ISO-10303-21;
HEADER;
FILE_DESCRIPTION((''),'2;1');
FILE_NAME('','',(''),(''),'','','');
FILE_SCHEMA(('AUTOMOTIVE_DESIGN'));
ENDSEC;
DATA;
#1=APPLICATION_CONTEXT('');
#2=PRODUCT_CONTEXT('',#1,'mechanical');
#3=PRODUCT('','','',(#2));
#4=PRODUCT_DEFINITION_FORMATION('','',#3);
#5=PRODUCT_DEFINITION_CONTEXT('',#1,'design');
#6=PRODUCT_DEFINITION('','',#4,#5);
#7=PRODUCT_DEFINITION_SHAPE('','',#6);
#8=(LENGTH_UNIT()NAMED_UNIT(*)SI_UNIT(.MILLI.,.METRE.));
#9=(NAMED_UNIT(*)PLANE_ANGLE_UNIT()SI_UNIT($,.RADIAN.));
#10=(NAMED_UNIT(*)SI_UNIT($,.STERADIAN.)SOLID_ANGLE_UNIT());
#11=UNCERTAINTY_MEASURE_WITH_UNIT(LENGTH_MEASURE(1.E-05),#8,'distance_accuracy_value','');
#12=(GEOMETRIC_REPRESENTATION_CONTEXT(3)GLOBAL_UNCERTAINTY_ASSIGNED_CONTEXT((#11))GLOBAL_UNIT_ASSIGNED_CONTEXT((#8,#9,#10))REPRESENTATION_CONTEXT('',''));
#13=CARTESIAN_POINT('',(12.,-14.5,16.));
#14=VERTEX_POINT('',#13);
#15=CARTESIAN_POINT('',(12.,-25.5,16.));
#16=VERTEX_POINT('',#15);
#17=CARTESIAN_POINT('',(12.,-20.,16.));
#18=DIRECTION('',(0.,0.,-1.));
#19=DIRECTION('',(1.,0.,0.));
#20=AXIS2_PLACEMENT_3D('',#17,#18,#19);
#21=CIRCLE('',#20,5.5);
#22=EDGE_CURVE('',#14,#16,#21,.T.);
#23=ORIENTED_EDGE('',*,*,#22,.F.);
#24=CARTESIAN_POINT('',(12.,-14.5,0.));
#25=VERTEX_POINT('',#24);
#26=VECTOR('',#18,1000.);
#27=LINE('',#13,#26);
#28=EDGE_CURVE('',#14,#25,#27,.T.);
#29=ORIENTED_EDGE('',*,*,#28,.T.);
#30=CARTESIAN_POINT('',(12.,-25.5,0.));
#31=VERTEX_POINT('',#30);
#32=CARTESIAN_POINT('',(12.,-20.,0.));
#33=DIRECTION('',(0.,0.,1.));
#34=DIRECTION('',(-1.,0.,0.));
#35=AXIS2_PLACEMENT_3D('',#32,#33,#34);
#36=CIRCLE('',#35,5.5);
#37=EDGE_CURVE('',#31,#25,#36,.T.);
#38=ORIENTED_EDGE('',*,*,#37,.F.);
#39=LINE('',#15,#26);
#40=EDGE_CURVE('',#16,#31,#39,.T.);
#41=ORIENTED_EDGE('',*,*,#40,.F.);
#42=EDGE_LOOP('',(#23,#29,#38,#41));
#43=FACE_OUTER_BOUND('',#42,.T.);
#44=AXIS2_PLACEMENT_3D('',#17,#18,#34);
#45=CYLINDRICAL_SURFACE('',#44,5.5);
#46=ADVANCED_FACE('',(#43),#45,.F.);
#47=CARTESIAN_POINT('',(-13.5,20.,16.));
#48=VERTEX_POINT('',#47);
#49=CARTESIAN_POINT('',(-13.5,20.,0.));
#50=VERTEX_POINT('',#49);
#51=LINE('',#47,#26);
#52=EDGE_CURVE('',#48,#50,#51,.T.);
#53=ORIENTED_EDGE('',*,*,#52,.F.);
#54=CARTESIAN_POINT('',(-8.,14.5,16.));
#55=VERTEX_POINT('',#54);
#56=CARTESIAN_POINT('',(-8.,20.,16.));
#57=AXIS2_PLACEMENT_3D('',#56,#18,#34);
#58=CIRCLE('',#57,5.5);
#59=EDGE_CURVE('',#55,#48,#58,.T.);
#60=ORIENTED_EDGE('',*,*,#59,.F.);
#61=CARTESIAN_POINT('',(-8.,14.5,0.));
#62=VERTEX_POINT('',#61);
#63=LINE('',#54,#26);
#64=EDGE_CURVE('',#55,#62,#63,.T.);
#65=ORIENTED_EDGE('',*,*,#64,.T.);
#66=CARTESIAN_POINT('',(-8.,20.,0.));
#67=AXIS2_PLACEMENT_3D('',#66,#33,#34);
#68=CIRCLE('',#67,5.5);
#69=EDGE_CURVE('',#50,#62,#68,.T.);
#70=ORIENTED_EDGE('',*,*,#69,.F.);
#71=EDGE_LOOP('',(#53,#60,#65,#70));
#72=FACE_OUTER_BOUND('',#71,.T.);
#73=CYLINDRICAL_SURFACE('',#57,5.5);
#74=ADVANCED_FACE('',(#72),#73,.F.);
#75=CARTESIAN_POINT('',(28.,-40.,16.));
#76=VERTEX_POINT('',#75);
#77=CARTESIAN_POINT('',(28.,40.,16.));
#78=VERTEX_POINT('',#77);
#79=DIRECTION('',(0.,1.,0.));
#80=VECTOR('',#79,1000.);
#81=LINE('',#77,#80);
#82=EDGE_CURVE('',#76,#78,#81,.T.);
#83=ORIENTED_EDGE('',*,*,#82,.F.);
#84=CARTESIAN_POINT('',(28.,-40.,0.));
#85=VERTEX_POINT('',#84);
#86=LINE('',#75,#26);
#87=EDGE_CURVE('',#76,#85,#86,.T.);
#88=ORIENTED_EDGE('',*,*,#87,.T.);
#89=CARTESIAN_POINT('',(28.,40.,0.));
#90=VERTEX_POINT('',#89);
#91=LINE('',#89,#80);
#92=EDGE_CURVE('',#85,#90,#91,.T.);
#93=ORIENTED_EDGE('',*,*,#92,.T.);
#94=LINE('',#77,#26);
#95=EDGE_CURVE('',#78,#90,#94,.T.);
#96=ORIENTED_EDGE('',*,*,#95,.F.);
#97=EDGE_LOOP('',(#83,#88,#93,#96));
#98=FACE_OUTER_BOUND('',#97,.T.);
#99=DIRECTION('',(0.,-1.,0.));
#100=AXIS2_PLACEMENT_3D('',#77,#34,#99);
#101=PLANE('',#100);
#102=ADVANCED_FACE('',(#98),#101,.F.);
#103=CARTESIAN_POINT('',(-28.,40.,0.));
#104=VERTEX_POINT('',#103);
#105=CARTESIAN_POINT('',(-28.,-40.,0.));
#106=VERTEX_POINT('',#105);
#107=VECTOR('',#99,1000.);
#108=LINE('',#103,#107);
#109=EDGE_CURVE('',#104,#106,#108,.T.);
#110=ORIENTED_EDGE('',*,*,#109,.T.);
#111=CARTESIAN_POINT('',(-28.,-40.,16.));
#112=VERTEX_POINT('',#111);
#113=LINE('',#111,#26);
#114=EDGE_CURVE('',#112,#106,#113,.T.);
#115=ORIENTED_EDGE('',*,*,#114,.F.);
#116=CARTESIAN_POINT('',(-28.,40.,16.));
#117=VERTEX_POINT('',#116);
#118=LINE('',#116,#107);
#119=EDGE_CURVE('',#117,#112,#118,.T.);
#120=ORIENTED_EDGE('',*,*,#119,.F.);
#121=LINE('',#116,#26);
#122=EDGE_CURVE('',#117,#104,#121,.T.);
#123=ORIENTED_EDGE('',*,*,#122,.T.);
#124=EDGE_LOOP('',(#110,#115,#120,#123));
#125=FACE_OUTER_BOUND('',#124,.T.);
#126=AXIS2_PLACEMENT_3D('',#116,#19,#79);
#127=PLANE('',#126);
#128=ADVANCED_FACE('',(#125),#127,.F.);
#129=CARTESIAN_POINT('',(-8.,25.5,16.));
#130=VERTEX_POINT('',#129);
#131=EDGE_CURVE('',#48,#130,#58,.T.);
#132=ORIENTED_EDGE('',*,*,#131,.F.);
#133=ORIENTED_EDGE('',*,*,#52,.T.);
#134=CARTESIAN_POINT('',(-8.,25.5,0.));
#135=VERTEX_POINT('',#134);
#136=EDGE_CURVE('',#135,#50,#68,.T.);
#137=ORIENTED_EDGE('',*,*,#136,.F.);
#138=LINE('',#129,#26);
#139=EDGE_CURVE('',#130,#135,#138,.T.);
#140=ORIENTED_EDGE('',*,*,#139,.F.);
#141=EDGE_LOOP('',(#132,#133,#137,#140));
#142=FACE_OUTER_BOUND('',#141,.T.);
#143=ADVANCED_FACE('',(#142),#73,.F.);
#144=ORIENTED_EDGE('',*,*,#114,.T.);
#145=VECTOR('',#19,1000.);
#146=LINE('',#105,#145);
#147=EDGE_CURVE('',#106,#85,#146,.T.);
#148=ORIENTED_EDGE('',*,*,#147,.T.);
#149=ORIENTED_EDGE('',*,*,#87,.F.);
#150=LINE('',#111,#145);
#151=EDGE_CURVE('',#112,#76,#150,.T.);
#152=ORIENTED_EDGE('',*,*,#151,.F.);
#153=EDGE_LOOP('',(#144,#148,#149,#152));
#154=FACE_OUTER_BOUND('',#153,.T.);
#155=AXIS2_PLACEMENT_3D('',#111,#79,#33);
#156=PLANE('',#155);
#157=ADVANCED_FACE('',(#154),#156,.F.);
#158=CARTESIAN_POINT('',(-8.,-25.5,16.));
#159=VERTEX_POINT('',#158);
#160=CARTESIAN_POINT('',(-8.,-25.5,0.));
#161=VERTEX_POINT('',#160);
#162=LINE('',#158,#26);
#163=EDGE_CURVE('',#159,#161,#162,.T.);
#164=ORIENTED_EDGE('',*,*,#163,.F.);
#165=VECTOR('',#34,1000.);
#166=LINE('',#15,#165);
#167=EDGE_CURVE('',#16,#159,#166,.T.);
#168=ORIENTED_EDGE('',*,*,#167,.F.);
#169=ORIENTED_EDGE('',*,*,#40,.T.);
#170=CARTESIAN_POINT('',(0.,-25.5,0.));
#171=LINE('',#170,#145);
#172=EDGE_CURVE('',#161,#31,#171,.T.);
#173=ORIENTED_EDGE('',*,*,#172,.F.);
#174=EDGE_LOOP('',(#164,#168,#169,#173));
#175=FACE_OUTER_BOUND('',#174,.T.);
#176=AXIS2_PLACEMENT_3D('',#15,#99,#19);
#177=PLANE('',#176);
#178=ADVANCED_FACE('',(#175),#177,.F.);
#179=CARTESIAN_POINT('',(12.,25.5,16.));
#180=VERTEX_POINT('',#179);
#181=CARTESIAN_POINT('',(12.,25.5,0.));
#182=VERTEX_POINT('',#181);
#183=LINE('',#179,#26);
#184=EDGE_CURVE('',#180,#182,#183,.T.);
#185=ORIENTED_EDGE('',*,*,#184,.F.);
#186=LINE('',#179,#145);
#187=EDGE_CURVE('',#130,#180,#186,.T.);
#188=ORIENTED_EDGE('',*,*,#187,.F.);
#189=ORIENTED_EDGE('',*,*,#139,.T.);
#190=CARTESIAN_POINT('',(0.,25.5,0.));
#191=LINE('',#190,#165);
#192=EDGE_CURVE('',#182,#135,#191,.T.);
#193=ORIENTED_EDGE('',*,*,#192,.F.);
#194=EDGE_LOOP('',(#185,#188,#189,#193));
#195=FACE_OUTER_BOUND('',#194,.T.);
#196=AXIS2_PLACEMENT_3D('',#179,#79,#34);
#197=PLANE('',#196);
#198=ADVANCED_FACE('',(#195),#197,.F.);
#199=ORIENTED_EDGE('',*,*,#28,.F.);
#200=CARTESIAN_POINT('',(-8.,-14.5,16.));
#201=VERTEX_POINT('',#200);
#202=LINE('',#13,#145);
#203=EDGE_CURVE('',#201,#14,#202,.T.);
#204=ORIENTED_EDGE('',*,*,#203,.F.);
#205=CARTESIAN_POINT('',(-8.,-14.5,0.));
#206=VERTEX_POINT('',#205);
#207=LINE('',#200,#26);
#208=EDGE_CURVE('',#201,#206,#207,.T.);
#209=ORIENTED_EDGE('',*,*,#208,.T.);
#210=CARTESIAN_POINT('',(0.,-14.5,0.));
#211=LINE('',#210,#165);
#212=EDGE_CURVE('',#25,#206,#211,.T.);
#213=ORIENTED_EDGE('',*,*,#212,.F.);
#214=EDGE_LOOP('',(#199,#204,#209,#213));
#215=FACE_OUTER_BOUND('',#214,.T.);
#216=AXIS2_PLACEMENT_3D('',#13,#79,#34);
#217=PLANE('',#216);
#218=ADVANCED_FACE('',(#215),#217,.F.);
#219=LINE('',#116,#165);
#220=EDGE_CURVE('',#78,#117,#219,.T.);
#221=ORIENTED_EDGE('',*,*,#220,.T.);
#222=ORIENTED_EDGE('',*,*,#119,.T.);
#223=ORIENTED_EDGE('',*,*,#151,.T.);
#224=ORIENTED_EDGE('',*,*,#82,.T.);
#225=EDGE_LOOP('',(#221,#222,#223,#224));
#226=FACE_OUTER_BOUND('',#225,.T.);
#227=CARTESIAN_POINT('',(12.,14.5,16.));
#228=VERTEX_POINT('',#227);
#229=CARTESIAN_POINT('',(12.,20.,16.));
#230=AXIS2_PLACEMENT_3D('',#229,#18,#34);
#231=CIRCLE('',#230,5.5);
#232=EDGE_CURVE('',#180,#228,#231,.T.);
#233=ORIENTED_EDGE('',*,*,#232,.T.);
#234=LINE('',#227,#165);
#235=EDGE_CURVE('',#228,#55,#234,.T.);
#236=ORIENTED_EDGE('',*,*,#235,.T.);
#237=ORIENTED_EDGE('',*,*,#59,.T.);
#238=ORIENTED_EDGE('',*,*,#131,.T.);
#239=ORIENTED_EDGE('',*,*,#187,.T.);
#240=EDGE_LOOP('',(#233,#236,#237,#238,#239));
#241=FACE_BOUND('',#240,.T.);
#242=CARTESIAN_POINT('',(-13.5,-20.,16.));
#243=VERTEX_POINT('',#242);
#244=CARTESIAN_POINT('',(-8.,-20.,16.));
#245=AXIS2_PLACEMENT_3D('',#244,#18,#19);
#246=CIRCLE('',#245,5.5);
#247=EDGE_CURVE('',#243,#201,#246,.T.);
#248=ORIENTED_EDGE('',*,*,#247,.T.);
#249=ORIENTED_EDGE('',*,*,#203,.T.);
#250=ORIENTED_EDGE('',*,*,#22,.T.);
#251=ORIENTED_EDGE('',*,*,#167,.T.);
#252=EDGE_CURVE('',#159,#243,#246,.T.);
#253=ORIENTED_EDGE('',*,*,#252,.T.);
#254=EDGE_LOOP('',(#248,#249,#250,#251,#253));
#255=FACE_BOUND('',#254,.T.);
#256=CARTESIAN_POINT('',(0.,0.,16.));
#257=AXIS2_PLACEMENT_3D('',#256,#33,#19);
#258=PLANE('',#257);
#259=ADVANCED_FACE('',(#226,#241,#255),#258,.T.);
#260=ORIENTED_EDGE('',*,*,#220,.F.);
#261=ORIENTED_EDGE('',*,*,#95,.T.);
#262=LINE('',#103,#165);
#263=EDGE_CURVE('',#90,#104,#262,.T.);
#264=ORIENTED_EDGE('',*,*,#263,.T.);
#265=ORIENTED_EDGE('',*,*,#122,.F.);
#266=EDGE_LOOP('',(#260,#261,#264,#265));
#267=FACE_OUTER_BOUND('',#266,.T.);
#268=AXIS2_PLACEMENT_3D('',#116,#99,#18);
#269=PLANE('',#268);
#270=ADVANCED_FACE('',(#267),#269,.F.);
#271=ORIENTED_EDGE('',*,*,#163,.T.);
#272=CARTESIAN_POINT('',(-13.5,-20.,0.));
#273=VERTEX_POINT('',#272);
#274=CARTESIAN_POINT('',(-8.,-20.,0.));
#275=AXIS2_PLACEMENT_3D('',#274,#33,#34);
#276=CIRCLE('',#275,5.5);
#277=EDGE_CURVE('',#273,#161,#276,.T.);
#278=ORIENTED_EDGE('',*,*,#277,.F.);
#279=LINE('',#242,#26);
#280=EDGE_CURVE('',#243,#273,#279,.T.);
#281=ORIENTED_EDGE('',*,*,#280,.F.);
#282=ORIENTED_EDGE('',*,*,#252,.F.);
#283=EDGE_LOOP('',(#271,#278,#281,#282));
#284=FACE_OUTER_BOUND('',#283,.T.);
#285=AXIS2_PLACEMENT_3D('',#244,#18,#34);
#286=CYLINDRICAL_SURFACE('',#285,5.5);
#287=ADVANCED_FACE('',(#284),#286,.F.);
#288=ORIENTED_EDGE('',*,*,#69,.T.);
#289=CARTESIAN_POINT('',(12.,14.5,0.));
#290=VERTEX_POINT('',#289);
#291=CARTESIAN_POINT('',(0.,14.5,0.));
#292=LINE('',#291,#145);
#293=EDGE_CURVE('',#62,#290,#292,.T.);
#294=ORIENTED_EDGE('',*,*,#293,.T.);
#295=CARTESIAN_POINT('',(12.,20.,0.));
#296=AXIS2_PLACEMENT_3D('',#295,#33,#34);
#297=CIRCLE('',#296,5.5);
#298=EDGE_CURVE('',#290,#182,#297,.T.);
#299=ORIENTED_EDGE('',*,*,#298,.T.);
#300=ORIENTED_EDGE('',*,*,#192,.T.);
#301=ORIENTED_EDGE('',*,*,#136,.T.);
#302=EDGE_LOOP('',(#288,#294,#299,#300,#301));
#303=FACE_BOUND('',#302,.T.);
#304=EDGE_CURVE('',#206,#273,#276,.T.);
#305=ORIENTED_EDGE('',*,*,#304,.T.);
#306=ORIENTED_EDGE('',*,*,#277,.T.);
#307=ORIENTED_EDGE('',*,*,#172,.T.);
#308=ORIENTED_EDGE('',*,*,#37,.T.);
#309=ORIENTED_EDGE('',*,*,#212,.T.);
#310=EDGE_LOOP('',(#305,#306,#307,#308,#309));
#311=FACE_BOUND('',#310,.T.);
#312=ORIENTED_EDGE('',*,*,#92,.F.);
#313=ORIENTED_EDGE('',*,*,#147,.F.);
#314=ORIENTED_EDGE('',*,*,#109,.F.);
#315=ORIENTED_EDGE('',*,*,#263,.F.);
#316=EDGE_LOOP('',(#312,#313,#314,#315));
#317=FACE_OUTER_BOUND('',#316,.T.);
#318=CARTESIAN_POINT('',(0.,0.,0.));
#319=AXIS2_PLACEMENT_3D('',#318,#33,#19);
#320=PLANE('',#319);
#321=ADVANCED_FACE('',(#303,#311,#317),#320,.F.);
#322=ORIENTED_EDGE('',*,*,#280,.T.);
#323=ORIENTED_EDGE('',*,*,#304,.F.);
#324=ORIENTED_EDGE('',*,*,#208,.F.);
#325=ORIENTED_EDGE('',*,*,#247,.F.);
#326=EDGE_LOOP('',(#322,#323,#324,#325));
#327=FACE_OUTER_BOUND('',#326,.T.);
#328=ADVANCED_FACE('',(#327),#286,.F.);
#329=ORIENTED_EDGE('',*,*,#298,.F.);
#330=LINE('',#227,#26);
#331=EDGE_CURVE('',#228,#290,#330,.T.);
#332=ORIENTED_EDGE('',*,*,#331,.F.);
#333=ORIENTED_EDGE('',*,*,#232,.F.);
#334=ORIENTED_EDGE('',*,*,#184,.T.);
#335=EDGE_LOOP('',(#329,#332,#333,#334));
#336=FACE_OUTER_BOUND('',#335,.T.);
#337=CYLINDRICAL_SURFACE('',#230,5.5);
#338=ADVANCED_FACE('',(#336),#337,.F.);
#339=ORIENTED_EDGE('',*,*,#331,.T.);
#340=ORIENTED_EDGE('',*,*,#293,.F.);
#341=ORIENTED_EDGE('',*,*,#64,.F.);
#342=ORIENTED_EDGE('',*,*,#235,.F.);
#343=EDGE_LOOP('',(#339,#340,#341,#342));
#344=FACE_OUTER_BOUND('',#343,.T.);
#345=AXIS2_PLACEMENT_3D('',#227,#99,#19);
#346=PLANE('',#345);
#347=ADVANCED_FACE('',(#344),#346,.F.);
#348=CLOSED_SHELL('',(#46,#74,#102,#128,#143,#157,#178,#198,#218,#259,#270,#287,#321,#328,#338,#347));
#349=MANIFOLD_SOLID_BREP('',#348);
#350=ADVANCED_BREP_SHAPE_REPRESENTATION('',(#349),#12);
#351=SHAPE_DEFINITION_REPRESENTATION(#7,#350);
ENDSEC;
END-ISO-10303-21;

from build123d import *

# Parameters (mm, degrees)
SKETCH_1_W               = 56
SKETCH_1_H               = 80
EXTRUDE_1_DEPTH          = 16
CUT_EXTRUDE_1_DEPTH      = 52.380930315
CUT_EXTRUDE_1_DEPTH_BACK = 52.380930315


with BuildPart() as part:
    # 草图1 → 凸台-拉伸1 (new body)
    with BuildSketch(Plane.XY):
        Rectangle(SKETCH_1_W, SKETCH_1_H)
    extrude(amount=EXTRUDE_1_DEPTH)

    # 草图2 → 切除-拉伸1 (cut, two sides: drawn at the far end of the back side and taken through both)
    with BuildSketch(Plane(origin=(0, 0, 0), x_dir=(-1, 0, 0), z_dir=(0, 0, -1)).offset(-CUT_EXTRUDE_1_DEPTH_BACK)):
        with BuildLine():
            Line((-12, 25.5), (8, 25.5))
            ThreePointArc((8, 25.5), (13.5, 20), (8, 14.5))
            Line((8, 14.5), (-12, 14.5))
            ThreePointArc((-12, 14.5), (-17.5, 20), (-12, 25.5))
        make_face()
        with BuildLine():
            Line((-12, -25.5), (8, -25.5))
            ThreePointArc((8, -25.5), (13.5, -20), (8, -14.5))
            Line((8, -14.5), (-12, -14.5))
            ThreePointArc((-12, -14.5), (-17.5, -20), (-12, -25.5))
        make_face()
    extrude(amount=CUT_EXTRUDE_1_DEPTH + CUT_EXTRUDE_1_DEPTH_BACK, mode=Mode.SUBTRACT)


solid = part.part
